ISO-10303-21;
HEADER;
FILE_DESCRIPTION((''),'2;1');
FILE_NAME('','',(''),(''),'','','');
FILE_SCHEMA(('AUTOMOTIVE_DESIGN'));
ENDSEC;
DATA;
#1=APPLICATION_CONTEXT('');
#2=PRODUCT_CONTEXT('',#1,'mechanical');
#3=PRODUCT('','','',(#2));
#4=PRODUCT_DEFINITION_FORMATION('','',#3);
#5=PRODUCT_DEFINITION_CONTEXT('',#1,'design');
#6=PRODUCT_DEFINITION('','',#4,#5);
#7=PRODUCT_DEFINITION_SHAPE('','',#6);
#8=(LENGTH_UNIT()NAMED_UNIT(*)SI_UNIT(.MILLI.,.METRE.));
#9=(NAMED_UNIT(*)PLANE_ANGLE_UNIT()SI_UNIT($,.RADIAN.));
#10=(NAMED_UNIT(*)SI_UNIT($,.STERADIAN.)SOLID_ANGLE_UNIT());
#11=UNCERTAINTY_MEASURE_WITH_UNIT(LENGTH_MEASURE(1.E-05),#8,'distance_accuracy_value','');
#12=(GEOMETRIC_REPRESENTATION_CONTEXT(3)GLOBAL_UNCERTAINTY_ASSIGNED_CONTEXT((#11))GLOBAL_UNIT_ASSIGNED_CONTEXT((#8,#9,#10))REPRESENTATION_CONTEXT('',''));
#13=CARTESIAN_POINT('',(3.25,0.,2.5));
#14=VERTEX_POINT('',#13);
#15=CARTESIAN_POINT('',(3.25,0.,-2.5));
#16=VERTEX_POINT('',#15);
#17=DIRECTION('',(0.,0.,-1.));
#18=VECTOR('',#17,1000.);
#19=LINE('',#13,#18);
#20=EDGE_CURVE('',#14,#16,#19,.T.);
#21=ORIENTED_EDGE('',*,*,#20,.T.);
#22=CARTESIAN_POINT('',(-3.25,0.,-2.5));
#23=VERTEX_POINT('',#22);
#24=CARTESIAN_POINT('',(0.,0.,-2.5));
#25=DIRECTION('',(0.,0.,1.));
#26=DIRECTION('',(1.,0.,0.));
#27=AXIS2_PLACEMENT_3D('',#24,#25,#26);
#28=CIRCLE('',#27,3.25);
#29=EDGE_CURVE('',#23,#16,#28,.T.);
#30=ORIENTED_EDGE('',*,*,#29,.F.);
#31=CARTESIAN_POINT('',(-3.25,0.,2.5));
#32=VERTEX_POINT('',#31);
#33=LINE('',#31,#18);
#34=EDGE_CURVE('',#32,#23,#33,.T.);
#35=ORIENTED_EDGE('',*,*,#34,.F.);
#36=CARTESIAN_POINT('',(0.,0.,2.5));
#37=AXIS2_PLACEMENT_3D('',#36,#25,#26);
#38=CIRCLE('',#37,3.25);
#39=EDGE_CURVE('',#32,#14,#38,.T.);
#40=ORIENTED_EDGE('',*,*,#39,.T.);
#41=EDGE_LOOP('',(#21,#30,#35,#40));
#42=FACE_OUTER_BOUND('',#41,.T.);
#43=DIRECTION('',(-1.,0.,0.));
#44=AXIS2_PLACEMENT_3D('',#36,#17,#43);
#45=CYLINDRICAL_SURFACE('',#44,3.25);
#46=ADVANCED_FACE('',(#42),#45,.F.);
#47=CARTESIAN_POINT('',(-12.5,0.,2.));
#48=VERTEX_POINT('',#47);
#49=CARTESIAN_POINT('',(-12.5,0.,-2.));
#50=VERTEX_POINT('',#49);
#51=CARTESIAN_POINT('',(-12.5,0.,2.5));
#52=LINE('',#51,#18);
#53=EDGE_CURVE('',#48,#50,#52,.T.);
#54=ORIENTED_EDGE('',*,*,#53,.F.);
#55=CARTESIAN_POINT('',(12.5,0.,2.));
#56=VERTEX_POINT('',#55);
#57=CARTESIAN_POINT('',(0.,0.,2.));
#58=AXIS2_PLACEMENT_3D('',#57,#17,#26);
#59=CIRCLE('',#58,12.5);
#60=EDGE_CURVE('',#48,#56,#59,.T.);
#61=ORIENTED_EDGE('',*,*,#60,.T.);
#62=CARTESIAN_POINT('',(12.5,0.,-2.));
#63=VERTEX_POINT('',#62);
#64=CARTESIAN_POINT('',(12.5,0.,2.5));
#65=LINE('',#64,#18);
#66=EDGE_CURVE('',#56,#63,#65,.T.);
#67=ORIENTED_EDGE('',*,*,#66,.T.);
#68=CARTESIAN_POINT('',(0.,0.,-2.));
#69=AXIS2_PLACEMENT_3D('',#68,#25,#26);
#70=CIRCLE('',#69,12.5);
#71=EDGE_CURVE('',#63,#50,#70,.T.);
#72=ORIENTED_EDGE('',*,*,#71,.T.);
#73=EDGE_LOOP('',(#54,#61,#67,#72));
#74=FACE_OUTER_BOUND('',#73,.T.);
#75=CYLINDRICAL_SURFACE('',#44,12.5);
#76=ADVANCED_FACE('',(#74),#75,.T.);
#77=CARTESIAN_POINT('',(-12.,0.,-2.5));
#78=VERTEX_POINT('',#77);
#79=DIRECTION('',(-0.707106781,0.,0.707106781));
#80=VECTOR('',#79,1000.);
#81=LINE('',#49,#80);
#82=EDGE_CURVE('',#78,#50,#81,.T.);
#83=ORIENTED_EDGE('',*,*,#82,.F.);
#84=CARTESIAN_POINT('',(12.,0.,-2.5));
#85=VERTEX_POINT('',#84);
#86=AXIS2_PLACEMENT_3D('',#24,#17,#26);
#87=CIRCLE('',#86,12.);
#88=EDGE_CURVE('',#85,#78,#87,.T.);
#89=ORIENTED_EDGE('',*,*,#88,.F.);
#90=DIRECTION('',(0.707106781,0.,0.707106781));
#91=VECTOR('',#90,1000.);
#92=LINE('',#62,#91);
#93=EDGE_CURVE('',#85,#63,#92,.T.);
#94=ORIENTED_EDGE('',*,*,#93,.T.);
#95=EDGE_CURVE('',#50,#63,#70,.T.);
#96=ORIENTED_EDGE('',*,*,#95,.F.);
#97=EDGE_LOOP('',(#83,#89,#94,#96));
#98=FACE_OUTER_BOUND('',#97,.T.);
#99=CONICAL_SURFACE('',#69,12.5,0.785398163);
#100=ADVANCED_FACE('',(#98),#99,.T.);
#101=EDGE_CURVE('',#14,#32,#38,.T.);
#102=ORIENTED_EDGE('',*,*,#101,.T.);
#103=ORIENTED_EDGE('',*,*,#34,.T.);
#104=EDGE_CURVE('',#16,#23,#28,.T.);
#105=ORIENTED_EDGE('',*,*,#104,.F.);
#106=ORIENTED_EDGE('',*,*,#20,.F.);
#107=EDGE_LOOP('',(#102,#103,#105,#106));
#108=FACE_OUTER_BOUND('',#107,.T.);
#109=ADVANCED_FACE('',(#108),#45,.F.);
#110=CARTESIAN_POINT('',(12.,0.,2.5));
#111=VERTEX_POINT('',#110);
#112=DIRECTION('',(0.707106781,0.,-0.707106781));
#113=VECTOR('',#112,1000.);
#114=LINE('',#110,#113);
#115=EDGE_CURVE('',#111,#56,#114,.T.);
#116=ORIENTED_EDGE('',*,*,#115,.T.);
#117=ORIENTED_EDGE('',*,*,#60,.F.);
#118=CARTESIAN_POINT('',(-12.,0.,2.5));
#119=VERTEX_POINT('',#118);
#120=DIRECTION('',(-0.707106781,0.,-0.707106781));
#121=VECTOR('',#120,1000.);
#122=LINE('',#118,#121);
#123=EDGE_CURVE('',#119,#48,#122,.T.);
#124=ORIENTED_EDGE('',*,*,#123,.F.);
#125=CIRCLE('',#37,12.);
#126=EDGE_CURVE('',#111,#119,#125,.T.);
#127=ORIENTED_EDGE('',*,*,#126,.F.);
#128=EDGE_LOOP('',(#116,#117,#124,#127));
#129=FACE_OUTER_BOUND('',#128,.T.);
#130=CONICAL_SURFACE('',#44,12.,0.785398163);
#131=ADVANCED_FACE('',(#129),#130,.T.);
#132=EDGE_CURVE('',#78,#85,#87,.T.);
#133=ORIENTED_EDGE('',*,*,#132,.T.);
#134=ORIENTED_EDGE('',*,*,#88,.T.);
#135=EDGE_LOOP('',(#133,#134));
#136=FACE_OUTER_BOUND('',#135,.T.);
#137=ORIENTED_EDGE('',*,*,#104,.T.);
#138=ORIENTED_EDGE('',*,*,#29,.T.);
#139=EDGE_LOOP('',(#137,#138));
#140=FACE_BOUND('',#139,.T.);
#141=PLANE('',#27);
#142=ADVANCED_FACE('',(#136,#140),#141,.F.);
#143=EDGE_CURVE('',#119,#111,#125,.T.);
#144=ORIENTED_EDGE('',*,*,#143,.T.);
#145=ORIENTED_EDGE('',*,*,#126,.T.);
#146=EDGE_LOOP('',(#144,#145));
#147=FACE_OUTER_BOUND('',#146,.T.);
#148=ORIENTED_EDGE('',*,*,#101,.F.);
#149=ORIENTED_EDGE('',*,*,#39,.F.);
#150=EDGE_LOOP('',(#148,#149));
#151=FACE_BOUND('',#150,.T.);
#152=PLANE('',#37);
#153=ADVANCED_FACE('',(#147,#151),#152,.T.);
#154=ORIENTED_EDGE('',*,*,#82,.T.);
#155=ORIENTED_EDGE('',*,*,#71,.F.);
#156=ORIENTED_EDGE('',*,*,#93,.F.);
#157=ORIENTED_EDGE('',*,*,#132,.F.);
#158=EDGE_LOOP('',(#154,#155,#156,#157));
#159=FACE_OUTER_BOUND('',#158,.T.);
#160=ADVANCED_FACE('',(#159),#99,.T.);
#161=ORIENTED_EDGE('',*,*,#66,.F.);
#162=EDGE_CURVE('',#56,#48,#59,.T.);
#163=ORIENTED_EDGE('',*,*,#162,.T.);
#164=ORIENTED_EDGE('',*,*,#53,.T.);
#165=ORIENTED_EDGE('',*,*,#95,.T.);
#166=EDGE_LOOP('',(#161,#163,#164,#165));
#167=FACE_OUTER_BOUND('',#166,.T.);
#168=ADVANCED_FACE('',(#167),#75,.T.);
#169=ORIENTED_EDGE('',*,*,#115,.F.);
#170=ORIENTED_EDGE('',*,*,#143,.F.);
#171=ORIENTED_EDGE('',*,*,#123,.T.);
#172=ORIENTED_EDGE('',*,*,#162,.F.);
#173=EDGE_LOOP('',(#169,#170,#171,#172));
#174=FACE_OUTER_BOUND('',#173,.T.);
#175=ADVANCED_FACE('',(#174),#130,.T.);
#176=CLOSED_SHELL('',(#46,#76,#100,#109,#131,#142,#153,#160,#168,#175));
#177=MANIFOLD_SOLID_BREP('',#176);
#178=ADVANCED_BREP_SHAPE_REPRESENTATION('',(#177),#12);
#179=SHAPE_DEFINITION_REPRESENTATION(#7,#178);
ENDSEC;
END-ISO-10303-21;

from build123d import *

# Parameters (mm, degrees)
SKETCH_1_R      = 12.5
SKETCH_1_R_2    = 3.25
EXTRUDE_1_DEPTH = 2.5
CHAMFER_1_SIZE  = 0.5


with BuildPart() as part:
    # 草图1 → 凸台-拉伸1 (new, symmetric)
    with BuildSketch(Plane.XY):
        Circle(SKETCH_1_R)
        Circle(SKETCH_1_R_2, mode=Mode.SUBTRACT)
    extrude(amount=EXTRUDE_1_DEPTH, both=True)

    # 倒角1
    chamfer_1_edges = [part.edges().sort_by_distance(p)[0] for p in [
        (-12.5, 0, -2.5),
        (-12.5, 0, 2.5),
    ]]
    chamfer(chamfer_1_edges, length=CHAMFER_1_SIZE)


solid = part.part
